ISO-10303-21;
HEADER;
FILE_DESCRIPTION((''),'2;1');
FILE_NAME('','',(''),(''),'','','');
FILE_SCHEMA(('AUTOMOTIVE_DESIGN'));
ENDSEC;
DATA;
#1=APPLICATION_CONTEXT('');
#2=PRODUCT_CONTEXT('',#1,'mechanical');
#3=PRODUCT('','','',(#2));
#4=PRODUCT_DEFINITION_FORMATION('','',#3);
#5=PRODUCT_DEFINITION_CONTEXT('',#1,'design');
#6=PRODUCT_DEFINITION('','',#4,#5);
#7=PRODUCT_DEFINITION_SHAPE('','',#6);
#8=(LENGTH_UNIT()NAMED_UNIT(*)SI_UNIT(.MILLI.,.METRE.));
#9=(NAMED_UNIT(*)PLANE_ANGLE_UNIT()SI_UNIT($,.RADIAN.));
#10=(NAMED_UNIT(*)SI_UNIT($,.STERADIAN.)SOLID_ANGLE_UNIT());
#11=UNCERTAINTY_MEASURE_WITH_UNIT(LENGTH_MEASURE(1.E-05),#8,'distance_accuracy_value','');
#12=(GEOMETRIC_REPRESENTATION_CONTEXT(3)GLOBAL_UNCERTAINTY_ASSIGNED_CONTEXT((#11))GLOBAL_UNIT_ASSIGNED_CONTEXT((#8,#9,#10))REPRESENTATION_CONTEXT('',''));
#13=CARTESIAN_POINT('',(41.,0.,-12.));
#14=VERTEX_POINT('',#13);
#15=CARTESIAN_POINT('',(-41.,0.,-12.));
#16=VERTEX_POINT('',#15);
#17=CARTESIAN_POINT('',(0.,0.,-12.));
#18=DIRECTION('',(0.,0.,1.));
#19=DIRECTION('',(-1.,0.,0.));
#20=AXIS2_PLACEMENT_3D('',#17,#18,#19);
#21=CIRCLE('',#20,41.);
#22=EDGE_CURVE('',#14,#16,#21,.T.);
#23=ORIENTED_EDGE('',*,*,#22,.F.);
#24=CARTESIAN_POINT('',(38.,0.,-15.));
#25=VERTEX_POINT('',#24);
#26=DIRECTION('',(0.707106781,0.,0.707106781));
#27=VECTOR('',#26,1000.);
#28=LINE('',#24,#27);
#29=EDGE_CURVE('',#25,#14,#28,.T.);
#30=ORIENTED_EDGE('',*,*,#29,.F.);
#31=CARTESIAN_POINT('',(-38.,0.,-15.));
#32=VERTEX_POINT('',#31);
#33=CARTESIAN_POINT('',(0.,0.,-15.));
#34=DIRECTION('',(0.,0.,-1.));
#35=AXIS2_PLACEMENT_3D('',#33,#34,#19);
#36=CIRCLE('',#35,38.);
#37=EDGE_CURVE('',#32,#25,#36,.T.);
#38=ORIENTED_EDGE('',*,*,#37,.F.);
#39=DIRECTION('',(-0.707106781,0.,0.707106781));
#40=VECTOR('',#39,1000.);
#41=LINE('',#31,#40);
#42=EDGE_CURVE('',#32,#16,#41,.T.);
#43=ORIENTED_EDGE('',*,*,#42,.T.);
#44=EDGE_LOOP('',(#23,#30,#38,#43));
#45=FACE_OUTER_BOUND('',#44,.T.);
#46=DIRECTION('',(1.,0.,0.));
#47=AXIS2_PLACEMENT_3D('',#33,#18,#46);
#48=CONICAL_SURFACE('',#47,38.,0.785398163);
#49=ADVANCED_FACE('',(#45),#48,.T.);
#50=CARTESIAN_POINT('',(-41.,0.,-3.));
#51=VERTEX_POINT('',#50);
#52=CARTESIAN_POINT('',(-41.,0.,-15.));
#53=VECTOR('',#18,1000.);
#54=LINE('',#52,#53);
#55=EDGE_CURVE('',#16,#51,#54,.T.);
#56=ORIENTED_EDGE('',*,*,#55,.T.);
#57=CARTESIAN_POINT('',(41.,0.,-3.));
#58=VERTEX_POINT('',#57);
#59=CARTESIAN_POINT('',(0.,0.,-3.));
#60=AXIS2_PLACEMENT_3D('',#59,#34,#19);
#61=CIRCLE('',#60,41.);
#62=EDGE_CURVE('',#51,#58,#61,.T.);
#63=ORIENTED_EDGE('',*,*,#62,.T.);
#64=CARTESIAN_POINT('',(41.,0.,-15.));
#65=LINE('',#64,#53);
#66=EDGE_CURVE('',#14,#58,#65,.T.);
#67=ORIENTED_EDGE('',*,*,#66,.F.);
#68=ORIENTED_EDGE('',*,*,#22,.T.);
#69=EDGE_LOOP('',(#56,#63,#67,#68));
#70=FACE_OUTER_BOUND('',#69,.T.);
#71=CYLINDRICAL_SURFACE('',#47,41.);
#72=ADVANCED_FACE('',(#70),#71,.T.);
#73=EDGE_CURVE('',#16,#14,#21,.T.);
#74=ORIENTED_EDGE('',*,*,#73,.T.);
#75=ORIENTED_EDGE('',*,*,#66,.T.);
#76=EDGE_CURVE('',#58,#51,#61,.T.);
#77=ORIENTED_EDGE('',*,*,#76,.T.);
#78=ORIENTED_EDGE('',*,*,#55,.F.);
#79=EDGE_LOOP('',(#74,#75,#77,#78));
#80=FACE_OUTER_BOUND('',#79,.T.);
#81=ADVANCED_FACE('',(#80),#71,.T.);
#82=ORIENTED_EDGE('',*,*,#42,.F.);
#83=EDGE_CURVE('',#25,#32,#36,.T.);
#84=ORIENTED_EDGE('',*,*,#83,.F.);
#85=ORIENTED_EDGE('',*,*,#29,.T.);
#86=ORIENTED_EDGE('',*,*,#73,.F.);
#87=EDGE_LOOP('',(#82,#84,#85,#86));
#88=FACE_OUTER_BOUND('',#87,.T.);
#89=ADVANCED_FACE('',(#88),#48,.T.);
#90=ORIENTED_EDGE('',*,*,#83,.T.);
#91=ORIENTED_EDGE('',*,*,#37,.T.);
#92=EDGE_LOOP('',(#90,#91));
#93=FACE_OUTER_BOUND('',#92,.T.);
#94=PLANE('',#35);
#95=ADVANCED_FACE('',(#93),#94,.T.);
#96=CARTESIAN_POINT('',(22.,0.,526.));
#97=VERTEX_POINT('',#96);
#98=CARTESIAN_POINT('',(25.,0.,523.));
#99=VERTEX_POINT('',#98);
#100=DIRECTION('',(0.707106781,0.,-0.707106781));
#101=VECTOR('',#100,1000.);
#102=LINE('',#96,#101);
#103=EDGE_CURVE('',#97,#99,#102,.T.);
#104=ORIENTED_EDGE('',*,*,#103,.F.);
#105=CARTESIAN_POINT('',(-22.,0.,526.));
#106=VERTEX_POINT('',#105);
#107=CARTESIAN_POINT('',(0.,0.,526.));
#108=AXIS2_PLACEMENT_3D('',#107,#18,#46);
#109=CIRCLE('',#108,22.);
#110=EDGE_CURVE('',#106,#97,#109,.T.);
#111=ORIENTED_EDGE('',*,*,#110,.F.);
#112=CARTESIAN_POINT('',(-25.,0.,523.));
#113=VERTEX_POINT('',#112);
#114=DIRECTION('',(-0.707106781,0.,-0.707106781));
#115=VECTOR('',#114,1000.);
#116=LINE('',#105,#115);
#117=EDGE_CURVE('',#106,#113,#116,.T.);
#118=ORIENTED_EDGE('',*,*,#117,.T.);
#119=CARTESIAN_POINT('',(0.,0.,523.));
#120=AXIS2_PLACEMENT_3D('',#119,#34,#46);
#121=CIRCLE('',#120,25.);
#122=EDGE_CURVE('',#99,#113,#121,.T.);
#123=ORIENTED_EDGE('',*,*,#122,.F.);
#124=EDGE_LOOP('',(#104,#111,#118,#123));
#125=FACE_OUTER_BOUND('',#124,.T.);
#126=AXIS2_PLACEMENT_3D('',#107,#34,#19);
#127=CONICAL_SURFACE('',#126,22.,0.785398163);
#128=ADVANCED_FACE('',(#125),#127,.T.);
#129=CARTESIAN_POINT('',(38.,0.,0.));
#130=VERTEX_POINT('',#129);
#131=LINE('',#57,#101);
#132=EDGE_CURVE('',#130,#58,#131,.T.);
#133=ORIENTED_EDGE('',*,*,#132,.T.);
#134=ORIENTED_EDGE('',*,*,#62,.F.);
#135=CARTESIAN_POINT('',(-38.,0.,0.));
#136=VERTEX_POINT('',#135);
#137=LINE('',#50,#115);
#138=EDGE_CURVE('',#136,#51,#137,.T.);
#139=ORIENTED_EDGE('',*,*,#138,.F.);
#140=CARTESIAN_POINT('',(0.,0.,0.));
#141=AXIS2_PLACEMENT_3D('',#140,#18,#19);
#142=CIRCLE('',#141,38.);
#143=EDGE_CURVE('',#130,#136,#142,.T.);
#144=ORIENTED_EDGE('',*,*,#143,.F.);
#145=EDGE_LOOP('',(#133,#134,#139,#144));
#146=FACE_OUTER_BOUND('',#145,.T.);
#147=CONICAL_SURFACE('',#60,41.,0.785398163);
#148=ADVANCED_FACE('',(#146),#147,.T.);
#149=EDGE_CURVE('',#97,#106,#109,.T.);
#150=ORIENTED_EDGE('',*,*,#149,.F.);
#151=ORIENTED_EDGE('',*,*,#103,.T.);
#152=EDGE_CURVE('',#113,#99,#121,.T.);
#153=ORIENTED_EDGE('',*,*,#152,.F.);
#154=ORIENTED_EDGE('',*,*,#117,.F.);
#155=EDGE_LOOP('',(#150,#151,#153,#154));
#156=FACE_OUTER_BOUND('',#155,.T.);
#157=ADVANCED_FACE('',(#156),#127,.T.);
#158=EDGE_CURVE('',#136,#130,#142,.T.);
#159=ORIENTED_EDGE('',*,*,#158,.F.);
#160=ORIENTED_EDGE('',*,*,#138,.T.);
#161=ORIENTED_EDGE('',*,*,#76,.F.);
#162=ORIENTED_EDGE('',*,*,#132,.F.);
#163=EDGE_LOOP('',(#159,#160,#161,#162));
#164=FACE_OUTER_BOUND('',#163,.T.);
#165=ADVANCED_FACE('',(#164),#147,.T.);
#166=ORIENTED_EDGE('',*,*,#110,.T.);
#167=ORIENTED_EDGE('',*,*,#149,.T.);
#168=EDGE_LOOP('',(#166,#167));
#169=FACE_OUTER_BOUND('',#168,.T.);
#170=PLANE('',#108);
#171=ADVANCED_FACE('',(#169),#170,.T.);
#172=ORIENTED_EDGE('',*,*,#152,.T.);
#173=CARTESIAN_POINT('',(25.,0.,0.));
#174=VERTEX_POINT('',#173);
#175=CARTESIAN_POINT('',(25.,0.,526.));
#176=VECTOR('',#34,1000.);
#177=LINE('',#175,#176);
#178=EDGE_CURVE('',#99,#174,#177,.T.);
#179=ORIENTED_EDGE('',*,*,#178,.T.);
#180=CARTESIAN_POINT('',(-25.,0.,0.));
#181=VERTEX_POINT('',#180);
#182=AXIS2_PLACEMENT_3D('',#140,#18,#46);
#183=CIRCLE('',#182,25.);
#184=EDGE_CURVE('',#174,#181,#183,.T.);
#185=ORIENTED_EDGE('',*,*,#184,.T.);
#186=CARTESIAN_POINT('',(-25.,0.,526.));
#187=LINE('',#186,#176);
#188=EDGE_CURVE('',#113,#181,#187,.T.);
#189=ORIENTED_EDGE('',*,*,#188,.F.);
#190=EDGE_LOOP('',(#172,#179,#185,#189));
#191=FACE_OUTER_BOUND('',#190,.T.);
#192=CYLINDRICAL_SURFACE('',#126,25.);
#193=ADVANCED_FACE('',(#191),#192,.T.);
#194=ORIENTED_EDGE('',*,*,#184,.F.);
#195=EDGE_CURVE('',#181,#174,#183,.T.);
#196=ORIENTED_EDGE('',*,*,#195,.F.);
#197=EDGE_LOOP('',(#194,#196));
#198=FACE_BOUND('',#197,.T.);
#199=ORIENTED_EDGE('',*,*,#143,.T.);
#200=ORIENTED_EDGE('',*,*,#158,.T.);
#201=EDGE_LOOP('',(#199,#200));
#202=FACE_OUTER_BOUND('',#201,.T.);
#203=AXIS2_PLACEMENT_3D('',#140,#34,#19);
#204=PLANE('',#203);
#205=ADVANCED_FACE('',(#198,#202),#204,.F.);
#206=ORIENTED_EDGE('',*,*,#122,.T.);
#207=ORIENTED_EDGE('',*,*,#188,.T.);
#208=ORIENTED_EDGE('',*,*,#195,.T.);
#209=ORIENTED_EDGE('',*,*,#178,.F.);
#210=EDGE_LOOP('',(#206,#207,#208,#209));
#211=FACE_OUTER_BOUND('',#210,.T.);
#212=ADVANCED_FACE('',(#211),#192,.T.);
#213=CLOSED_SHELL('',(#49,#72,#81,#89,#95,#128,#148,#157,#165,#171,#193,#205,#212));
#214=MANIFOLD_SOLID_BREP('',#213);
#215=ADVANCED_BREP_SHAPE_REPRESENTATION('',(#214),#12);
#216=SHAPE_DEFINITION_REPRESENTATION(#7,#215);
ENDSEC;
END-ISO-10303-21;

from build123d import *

# Parameters (mm, degrees)
SKETCH1_R           = 25
BOSS_EXTRUDE1_DEPTH = 526
SKETCH2_R           = 41
BOSS_EXTRUDE2_DEPTH = 15
CHAMFER1_SIZE       = 3


with BuildPart() as part:
    # Sketch1 → Boss-Extrude1 (new body)
    with BuildSketch(Plane.XY):
        Circle(SKETCH1_R)
    extrude(amount=BOSS_EXTRUDE1_DEPTH)

    # Sketch2 → Boss-Extrude2 (add)
    with BuildSketch(Plane(origin=(0, 0, 0), x_dir=(-1, 0, 0), z_dir=(0, 0, -1))):
        Circle(SKETCH2_R)
    extrude(amount=BOSS_EXTRUDE2_DEPTH)

    # Chamfer1
    chamfer1_edges = [part.edges().sort_by_distance(p)[0] for p in [
        (-25, 0, 526),
        (41, 0, 0),
        (41, 0, -15),
    ]]
    chamfer(chamfer1_edges, length=CHAMFER1_SIZE)


solid = part.part
